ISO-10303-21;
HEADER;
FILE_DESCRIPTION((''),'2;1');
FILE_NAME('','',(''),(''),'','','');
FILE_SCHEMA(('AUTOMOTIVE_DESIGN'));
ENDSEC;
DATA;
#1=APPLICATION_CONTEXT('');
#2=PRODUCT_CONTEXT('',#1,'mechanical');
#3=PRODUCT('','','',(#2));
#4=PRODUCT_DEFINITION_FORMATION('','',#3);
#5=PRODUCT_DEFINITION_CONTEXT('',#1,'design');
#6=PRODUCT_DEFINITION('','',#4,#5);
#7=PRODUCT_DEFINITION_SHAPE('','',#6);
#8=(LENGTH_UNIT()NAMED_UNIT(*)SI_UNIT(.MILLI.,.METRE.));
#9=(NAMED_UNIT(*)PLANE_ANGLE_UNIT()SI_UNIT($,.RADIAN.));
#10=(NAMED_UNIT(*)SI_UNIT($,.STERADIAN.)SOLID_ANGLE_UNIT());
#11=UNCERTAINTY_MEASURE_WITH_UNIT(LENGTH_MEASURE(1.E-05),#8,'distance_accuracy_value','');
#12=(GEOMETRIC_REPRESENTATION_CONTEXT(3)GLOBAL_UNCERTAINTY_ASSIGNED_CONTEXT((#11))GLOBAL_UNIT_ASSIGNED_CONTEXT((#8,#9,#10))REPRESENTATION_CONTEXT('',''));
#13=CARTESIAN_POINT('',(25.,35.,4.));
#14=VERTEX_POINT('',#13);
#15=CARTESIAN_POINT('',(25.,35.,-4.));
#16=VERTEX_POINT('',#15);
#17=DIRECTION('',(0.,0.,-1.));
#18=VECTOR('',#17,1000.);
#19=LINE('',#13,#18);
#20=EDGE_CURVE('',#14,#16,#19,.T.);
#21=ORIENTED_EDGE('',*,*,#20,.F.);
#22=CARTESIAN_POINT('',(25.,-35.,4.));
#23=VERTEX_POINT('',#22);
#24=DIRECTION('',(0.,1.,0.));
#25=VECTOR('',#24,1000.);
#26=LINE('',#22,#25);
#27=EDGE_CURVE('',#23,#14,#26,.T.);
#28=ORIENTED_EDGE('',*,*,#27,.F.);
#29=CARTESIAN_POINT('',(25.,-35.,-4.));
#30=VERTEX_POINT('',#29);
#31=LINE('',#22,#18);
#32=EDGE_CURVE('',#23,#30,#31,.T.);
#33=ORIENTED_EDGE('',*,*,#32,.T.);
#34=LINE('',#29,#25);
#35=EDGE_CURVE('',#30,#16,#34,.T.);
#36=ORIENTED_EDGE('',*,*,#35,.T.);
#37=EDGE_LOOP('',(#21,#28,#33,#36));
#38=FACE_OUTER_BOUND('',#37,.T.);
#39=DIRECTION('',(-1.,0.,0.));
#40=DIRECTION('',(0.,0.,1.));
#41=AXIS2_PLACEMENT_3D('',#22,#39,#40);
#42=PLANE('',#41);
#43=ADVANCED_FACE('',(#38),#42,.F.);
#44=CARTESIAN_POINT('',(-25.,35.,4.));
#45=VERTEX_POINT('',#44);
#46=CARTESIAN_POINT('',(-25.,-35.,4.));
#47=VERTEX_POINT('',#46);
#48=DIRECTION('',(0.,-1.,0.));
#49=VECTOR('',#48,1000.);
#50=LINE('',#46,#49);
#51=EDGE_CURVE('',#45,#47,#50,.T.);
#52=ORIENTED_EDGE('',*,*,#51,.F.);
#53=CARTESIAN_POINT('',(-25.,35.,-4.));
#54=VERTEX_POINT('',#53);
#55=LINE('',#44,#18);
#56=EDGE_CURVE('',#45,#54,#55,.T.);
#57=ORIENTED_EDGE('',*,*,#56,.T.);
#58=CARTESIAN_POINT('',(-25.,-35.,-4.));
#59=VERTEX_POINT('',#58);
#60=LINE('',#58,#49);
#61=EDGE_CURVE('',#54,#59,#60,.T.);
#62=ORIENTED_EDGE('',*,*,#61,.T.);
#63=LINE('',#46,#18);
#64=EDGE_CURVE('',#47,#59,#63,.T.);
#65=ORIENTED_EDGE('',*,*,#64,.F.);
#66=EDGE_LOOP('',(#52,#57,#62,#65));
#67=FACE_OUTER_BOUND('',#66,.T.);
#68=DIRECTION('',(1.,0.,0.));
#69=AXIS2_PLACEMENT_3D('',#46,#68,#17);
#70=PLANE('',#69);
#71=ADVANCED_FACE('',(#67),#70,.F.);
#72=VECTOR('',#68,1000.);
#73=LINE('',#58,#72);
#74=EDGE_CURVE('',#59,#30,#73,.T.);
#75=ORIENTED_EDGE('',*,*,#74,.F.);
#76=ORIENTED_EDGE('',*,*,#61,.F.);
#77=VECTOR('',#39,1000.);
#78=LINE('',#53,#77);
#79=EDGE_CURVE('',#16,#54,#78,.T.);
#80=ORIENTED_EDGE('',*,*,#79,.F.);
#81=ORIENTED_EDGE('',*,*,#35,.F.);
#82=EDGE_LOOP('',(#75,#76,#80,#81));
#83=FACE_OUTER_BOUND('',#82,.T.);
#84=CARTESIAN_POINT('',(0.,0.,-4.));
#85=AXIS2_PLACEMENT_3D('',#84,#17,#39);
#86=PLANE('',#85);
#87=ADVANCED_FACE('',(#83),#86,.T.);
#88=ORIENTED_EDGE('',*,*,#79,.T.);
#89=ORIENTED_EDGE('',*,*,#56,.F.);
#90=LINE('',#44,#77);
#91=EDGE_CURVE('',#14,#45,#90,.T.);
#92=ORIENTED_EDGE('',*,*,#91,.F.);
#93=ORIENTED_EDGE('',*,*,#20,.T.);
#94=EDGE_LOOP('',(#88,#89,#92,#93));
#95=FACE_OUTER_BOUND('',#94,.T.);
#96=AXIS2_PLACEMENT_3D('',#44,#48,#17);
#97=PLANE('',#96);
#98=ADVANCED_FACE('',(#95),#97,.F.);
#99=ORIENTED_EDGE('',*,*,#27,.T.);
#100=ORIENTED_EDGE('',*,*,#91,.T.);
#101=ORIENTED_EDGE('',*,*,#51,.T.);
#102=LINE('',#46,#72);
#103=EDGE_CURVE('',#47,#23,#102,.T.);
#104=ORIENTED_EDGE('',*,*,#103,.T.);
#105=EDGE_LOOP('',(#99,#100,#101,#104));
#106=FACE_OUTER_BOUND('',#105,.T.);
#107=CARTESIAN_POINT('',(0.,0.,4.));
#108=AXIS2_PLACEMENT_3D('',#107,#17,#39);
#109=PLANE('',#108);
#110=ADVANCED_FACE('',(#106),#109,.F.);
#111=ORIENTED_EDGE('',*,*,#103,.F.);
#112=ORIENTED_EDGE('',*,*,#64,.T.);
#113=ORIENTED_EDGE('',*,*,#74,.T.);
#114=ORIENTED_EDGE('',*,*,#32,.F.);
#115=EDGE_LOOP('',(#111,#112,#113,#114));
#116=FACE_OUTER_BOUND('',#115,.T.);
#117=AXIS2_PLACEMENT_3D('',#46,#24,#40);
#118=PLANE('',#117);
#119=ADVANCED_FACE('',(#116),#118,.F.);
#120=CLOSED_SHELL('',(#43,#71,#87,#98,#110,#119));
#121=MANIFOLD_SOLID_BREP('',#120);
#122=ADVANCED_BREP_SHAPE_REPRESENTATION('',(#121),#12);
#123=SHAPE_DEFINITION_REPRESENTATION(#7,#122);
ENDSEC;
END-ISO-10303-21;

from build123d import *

# Parameters (mm, degrees)
SKETCH_1_W      = 50
SKETCH_1_H      = 70
EXTRUDE_1_DEPTH = 4


with BuildPart() as part:
    # 草图1 → 凸台-拉伸1 (new, symmetric)
    with BuildSketch(Plane.XY):
        Rectangle(SKETCH_1_W, SKETCH_1_H)
    extrude(amount=EXTRUDE_1_DEPTH, both=True)


solid = part.part
